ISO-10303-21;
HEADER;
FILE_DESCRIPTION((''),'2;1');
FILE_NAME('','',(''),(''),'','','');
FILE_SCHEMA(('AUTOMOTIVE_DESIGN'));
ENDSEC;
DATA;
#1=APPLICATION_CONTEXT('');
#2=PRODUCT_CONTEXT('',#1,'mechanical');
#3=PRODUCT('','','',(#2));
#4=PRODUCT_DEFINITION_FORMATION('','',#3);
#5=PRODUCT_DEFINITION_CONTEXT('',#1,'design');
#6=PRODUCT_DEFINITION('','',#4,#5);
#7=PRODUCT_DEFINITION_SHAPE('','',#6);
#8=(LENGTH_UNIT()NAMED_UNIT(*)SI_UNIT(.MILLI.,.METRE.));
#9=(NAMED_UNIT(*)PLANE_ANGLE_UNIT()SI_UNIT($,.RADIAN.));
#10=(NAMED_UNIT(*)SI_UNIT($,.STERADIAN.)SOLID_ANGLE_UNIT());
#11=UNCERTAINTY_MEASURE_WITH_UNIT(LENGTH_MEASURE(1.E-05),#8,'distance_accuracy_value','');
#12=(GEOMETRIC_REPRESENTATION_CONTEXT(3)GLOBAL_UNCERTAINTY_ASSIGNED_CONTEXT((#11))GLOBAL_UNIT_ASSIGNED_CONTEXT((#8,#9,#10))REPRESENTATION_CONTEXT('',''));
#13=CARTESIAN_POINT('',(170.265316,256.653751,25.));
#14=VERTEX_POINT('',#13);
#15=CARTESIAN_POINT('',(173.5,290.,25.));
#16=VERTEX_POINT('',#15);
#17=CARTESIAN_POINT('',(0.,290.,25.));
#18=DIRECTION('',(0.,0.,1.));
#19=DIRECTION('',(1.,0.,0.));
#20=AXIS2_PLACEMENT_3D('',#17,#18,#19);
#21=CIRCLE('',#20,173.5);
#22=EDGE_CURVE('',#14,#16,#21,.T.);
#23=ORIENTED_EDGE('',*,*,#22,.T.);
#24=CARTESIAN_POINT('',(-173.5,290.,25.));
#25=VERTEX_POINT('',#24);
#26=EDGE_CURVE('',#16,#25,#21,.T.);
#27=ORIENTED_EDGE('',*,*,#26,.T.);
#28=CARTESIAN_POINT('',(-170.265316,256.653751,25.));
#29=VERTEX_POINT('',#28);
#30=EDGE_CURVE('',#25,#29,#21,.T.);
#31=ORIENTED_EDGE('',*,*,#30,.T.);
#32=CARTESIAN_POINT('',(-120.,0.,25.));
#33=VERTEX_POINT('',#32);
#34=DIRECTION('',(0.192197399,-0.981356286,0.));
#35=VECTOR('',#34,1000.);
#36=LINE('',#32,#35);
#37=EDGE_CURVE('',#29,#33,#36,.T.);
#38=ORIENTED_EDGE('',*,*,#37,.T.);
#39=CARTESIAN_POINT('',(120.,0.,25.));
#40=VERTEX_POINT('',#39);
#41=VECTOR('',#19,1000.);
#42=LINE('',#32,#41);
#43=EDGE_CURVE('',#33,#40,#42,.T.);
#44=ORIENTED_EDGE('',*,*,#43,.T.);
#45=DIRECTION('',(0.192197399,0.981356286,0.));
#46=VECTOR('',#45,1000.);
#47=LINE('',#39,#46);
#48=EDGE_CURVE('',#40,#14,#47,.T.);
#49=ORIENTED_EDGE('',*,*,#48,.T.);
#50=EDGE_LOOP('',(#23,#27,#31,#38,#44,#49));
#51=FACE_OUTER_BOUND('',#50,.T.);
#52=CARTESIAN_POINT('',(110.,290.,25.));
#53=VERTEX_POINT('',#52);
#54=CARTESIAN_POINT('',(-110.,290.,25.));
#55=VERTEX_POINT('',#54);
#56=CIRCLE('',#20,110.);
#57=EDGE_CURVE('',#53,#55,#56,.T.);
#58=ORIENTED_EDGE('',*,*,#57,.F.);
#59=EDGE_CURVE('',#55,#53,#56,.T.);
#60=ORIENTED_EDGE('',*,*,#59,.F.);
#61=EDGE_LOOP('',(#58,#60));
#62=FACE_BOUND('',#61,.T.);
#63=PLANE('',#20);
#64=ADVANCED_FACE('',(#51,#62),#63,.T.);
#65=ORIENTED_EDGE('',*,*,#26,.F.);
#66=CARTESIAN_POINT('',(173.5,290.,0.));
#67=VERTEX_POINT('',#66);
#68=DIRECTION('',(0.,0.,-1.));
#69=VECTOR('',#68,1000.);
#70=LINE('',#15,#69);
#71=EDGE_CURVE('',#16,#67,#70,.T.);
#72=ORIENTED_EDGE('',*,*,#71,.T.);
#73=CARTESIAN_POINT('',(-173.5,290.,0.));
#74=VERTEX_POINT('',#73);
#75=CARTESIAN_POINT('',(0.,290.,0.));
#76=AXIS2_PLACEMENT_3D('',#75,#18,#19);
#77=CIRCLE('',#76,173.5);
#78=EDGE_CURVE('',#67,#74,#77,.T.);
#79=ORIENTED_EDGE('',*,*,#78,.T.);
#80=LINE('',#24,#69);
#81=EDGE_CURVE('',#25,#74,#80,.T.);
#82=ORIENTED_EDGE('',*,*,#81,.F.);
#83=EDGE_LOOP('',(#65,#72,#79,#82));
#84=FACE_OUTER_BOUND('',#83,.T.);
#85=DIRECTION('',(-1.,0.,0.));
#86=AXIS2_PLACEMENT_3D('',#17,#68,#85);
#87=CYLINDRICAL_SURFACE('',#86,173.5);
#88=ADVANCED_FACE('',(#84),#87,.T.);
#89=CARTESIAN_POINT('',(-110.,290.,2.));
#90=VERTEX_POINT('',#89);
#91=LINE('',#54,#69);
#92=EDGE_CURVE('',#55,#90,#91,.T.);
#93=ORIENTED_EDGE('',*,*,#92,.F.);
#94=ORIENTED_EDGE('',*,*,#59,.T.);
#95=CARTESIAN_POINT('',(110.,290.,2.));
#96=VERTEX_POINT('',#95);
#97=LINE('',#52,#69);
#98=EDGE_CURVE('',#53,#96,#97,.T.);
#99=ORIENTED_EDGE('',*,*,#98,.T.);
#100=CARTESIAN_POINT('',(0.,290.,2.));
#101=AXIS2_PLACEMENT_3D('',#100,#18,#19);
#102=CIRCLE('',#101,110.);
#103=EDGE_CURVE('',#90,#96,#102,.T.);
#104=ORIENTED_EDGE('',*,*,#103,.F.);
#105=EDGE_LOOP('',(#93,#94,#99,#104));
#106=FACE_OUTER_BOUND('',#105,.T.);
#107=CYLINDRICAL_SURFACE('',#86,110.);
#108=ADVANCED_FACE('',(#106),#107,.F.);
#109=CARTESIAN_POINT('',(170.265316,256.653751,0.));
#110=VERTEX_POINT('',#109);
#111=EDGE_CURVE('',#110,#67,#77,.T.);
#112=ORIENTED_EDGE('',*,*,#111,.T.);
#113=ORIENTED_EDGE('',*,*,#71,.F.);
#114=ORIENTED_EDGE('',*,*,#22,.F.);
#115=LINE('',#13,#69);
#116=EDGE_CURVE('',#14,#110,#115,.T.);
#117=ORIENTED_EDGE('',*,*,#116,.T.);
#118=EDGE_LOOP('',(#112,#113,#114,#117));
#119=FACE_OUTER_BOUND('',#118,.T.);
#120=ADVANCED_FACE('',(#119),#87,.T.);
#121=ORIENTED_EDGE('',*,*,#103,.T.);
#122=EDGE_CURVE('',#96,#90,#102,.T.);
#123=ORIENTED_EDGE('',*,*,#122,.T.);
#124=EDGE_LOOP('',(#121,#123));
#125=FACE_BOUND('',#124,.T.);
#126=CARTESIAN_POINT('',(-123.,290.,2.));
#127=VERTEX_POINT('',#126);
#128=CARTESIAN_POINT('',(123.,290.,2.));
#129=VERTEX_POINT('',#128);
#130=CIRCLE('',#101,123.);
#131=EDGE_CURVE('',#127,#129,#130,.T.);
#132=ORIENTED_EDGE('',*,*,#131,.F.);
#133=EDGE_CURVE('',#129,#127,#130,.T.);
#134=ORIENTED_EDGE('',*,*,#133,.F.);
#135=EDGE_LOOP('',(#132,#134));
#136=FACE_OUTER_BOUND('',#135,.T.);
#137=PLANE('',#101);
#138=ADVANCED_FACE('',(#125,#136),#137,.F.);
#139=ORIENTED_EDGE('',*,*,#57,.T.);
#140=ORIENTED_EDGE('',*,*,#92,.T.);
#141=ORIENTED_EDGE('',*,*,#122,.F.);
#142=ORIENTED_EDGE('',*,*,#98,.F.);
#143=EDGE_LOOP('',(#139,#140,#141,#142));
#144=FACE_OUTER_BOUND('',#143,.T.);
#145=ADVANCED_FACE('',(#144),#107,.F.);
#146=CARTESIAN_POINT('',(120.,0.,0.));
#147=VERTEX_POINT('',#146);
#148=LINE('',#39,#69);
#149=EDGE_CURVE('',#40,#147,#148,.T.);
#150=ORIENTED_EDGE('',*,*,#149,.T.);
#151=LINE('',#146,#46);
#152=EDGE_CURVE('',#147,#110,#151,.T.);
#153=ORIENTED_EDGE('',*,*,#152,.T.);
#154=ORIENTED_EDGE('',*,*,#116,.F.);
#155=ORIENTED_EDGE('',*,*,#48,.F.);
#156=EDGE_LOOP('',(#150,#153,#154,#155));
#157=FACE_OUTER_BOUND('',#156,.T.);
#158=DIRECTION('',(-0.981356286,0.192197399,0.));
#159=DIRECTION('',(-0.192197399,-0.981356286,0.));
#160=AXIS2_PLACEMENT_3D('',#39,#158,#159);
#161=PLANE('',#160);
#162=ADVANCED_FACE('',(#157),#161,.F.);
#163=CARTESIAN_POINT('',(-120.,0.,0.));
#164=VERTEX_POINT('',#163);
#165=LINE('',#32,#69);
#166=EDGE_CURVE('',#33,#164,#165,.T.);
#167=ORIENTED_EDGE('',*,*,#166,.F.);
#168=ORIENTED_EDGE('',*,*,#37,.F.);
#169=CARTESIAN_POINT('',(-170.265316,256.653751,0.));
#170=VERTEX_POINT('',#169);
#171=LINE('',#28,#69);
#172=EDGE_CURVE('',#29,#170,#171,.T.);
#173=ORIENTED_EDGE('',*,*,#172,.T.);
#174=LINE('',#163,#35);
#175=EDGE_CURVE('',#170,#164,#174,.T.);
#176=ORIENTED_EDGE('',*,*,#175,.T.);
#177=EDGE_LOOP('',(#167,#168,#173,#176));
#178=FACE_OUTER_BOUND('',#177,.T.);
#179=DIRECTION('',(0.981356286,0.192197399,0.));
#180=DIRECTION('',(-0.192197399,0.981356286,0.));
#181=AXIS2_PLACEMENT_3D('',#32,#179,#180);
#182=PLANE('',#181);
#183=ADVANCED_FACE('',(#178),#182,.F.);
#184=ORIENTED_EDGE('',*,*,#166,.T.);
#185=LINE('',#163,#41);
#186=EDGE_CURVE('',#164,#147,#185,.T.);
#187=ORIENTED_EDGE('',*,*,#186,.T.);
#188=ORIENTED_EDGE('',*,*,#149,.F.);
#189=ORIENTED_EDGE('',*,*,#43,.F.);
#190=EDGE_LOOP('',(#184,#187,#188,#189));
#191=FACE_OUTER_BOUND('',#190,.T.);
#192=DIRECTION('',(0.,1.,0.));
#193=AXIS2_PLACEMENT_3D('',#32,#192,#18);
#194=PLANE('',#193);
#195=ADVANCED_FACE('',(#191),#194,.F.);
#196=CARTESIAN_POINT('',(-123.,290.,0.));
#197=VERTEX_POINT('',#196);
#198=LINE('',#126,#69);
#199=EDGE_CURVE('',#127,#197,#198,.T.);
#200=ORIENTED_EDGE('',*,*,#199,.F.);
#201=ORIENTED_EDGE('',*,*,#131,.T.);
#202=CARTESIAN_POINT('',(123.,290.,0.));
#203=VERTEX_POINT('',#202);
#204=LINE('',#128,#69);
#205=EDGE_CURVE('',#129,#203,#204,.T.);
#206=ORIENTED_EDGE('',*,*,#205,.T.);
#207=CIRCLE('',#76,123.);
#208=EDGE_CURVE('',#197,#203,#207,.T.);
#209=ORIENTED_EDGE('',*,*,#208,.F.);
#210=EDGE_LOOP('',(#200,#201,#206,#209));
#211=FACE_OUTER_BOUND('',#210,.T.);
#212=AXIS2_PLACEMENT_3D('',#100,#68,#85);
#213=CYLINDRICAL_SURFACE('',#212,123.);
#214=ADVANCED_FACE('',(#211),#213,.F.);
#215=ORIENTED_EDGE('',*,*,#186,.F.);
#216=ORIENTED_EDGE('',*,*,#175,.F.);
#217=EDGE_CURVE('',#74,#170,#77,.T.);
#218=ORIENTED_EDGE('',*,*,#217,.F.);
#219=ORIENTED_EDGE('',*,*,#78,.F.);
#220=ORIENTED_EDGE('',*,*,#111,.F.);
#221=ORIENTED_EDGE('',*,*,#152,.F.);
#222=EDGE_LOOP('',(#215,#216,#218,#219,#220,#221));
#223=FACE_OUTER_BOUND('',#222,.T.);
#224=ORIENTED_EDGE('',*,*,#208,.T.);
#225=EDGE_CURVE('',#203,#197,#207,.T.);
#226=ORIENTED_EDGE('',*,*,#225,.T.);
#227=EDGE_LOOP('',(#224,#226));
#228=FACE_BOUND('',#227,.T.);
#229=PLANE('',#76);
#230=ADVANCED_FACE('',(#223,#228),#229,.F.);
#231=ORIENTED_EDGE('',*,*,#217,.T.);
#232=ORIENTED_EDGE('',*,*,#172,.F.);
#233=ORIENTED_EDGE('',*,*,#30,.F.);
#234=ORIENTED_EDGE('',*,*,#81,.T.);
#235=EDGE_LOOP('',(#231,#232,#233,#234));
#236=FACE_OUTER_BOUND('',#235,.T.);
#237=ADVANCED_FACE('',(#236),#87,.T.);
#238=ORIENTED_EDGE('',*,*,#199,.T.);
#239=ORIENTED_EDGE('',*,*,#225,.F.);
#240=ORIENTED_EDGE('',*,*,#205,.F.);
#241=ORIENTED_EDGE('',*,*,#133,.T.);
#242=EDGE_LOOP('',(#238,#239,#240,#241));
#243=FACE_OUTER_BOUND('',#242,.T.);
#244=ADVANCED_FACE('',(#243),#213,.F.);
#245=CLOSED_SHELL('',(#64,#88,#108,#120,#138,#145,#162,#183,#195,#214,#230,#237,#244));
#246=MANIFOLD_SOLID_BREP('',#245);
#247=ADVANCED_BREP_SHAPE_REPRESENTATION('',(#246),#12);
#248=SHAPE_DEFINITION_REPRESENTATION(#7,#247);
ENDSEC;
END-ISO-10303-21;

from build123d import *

# Parameters (mm, degrees)
SKETCH1_R           = 110
BOSS_EXTRUDE1_DEPTH = 25
SKETCH2_R           = 123
SKETCH2_R_2         = 110
CUT_EXTRUDE2_DEPTH  = 2


with BuildPart() as part:
    # Sketch1 → Boss-Extrude1 (new body)
    with BuildSketch(Plane.XY):
        with BuildLine():
            Line((-120, 0), (120, 0))
            Line((120, 0), (170.2653156, 256.653751283))
            ThreePointArc((170.2653156, 256.653751283), (0, 463.5), (-170.2653156, 256.653751283))
            Line((-170.2653156, 256.653751283), (-120, 0))
        make_face()
        with Locations((0, 290)):
            Circle(SKETCH1_R, mode=Mode.SUBTRACT)
    extrude(amount=BOSS_EXTRUDE1_DEPTH)

    # Sketch2 → Cut-Extrude2 (cut)
    with BuildSketch(Plane.XY):
        with Locations((0, 290)):
            Circle(SKETCH2_R)
        with Locations((0, 290)):
            Circle(SKETCH2_R_2, mode=Mode.SUBTRACT)
    extrude(amount=CUT_EXTRUDE2_DEPTH, mode=Mode.SUBTRACT)


solid = part.part
